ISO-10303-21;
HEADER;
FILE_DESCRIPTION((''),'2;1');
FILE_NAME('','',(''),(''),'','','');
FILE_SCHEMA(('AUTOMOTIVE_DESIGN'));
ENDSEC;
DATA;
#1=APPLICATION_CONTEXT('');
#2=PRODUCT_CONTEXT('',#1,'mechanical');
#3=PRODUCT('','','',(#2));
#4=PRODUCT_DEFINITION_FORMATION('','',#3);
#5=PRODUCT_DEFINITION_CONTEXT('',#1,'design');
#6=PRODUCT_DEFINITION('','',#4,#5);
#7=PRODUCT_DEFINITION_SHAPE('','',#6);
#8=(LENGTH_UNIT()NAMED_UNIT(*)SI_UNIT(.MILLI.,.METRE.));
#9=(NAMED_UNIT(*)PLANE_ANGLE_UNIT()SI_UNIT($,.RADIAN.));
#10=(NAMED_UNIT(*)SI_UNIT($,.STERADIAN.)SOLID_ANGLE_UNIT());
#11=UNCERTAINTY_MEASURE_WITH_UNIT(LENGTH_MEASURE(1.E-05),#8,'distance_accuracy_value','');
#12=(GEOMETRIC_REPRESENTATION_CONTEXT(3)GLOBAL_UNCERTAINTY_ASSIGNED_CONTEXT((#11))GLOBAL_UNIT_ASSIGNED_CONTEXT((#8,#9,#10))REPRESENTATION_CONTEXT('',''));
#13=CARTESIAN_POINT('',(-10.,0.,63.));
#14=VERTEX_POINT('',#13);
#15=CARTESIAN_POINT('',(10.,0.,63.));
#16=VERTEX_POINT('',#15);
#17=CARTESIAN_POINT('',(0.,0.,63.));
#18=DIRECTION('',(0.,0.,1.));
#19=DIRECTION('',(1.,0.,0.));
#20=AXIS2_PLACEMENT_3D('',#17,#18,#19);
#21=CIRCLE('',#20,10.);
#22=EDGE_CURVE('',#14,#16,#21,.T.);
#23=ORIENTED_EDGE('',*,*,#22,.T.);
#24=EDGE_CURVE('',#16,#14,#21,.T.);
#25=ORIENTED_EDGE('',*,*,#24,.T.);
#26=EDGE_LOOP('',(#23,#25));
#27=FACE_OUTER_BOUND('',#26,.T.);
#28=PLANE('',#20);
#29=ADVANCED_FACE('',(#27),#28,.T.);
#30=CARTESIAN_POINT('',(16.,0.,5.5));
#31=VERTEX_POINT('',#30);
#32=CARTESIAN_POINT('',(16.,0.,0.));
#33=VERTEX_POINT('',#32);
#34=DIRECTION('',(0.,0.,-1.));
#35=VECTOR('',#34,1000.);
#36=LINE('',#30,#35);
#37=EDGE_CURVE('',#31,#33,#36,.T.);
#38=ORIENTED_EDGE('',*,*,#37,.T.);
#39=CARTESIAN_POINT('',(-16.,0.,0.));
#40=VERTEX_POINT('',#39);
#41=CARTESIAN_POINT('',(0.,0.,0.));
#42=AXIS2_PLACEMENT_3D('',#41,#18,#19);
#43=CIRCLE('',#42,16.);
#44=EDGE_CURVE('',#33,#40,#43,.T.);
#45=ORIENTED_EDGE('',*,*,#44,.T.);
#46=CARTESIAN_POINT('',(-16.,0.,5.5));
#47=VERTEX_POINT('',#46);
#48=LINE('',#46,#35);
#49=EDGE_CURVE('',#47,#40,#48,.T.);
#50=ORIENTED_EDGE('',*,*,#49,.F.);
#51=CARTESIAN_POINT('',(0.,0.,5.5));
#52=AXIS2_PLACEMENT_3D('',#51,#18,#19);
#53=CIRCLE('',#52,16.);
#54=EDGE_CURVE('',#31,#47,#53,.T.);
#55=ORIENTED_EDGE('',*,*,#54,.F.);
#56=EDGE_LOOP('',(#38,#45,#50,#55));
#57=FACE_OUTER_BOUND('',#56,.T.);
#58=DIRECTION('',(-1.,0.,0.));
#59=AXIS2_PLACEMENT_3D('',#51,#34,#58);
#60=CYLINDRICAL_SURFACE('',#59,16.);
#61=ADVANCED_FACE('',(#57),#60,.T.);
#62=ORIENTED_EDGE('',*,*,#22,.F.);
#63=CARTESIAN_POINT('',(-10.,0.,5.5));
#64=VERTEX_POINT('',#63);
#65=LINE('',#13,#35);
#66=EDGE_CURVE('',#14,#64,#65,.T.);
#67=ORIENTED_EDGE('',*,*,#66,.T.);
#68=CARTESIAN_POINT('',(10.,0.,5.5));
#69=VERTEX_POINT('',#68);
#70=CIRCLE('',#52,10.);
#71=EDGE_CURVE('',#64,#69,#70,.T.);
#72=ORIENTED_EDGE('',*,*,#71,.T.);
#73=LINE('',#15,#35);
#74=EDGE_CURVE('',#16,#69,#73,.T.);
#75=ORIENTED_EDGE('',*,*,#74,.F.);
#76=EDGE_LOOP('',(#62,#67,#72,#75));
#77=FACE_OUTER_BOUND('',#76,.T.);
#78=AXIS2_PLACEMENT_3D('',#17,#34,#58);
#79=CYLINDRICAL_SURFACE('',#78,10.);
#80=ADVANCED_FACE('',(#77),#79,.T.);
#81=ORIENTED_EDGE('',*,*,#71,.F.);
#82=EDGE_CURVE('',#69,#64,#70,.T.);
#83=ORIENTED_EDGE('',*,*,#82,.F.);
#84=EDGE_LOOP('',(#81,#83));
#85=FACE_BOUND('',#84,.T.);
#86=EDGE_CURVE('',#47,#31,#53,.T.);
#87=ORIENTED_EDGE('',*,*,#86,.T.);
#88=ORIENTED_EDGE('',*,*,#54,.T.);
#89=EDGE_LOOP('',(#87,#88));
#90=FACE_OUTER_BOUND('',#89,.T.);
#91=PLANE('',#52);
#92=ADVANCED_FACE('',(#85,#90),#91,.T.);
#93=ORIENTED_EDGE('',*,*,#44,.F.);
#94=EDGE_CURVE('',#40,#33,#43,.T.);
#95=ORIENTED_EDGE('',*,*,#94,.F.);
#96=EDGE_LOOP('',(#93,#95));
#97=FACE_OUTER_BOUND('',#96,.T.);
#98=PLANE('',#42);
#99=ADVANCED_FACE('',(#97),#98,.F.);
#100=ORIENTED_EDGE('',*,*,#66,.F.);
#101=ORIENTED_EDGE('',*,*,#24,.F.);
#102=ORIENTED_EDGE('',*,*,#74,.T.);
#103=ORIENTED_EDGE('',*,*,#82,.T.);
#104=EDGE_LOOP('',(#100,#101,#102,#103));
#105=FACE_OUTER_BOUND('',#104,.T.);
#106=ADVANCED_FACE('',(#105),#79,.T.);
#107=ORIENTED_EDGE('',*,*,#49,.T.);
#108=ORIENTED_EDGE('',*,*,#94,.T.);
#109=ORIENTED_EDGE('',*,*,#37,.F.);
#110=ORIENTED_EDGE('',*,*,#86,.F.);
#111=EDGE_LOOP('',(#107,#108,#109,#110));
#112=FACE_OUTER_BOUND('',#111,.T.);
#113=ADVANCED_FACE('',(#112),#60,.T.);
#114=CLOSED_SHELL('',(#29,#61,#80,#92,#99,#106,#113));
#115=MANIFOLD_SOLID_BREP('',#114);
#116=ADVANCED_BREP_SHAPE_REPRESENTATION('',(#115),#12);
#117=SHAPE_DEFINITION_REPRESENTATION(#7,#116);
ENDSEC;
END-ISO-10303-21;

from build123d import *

# Parameters (mm, degrees)
SKETCH_1_R      = 10
EXTRUDE_1_DEPTH = 63
SKETCH_2_R      = 16
EXTRUDE_2_DEPTH = 5.5


with BuildPart() as part:
    # 草图1 → 凸台-拉伸1 (new body)
    with BuildSketch(Plane.XY):
        Circle(SKETCH_1_R)
    extrude(amount=EXTRUDE_1_DEPTH)

    # 草图2 → 凸台-拉伸2 (add)
    with BuildSketch(Plane.XY):
        Circle(SKETCH_2_R)
    extrude(amount=EXTRUDE_2_DEPTH)


solid = part.part
